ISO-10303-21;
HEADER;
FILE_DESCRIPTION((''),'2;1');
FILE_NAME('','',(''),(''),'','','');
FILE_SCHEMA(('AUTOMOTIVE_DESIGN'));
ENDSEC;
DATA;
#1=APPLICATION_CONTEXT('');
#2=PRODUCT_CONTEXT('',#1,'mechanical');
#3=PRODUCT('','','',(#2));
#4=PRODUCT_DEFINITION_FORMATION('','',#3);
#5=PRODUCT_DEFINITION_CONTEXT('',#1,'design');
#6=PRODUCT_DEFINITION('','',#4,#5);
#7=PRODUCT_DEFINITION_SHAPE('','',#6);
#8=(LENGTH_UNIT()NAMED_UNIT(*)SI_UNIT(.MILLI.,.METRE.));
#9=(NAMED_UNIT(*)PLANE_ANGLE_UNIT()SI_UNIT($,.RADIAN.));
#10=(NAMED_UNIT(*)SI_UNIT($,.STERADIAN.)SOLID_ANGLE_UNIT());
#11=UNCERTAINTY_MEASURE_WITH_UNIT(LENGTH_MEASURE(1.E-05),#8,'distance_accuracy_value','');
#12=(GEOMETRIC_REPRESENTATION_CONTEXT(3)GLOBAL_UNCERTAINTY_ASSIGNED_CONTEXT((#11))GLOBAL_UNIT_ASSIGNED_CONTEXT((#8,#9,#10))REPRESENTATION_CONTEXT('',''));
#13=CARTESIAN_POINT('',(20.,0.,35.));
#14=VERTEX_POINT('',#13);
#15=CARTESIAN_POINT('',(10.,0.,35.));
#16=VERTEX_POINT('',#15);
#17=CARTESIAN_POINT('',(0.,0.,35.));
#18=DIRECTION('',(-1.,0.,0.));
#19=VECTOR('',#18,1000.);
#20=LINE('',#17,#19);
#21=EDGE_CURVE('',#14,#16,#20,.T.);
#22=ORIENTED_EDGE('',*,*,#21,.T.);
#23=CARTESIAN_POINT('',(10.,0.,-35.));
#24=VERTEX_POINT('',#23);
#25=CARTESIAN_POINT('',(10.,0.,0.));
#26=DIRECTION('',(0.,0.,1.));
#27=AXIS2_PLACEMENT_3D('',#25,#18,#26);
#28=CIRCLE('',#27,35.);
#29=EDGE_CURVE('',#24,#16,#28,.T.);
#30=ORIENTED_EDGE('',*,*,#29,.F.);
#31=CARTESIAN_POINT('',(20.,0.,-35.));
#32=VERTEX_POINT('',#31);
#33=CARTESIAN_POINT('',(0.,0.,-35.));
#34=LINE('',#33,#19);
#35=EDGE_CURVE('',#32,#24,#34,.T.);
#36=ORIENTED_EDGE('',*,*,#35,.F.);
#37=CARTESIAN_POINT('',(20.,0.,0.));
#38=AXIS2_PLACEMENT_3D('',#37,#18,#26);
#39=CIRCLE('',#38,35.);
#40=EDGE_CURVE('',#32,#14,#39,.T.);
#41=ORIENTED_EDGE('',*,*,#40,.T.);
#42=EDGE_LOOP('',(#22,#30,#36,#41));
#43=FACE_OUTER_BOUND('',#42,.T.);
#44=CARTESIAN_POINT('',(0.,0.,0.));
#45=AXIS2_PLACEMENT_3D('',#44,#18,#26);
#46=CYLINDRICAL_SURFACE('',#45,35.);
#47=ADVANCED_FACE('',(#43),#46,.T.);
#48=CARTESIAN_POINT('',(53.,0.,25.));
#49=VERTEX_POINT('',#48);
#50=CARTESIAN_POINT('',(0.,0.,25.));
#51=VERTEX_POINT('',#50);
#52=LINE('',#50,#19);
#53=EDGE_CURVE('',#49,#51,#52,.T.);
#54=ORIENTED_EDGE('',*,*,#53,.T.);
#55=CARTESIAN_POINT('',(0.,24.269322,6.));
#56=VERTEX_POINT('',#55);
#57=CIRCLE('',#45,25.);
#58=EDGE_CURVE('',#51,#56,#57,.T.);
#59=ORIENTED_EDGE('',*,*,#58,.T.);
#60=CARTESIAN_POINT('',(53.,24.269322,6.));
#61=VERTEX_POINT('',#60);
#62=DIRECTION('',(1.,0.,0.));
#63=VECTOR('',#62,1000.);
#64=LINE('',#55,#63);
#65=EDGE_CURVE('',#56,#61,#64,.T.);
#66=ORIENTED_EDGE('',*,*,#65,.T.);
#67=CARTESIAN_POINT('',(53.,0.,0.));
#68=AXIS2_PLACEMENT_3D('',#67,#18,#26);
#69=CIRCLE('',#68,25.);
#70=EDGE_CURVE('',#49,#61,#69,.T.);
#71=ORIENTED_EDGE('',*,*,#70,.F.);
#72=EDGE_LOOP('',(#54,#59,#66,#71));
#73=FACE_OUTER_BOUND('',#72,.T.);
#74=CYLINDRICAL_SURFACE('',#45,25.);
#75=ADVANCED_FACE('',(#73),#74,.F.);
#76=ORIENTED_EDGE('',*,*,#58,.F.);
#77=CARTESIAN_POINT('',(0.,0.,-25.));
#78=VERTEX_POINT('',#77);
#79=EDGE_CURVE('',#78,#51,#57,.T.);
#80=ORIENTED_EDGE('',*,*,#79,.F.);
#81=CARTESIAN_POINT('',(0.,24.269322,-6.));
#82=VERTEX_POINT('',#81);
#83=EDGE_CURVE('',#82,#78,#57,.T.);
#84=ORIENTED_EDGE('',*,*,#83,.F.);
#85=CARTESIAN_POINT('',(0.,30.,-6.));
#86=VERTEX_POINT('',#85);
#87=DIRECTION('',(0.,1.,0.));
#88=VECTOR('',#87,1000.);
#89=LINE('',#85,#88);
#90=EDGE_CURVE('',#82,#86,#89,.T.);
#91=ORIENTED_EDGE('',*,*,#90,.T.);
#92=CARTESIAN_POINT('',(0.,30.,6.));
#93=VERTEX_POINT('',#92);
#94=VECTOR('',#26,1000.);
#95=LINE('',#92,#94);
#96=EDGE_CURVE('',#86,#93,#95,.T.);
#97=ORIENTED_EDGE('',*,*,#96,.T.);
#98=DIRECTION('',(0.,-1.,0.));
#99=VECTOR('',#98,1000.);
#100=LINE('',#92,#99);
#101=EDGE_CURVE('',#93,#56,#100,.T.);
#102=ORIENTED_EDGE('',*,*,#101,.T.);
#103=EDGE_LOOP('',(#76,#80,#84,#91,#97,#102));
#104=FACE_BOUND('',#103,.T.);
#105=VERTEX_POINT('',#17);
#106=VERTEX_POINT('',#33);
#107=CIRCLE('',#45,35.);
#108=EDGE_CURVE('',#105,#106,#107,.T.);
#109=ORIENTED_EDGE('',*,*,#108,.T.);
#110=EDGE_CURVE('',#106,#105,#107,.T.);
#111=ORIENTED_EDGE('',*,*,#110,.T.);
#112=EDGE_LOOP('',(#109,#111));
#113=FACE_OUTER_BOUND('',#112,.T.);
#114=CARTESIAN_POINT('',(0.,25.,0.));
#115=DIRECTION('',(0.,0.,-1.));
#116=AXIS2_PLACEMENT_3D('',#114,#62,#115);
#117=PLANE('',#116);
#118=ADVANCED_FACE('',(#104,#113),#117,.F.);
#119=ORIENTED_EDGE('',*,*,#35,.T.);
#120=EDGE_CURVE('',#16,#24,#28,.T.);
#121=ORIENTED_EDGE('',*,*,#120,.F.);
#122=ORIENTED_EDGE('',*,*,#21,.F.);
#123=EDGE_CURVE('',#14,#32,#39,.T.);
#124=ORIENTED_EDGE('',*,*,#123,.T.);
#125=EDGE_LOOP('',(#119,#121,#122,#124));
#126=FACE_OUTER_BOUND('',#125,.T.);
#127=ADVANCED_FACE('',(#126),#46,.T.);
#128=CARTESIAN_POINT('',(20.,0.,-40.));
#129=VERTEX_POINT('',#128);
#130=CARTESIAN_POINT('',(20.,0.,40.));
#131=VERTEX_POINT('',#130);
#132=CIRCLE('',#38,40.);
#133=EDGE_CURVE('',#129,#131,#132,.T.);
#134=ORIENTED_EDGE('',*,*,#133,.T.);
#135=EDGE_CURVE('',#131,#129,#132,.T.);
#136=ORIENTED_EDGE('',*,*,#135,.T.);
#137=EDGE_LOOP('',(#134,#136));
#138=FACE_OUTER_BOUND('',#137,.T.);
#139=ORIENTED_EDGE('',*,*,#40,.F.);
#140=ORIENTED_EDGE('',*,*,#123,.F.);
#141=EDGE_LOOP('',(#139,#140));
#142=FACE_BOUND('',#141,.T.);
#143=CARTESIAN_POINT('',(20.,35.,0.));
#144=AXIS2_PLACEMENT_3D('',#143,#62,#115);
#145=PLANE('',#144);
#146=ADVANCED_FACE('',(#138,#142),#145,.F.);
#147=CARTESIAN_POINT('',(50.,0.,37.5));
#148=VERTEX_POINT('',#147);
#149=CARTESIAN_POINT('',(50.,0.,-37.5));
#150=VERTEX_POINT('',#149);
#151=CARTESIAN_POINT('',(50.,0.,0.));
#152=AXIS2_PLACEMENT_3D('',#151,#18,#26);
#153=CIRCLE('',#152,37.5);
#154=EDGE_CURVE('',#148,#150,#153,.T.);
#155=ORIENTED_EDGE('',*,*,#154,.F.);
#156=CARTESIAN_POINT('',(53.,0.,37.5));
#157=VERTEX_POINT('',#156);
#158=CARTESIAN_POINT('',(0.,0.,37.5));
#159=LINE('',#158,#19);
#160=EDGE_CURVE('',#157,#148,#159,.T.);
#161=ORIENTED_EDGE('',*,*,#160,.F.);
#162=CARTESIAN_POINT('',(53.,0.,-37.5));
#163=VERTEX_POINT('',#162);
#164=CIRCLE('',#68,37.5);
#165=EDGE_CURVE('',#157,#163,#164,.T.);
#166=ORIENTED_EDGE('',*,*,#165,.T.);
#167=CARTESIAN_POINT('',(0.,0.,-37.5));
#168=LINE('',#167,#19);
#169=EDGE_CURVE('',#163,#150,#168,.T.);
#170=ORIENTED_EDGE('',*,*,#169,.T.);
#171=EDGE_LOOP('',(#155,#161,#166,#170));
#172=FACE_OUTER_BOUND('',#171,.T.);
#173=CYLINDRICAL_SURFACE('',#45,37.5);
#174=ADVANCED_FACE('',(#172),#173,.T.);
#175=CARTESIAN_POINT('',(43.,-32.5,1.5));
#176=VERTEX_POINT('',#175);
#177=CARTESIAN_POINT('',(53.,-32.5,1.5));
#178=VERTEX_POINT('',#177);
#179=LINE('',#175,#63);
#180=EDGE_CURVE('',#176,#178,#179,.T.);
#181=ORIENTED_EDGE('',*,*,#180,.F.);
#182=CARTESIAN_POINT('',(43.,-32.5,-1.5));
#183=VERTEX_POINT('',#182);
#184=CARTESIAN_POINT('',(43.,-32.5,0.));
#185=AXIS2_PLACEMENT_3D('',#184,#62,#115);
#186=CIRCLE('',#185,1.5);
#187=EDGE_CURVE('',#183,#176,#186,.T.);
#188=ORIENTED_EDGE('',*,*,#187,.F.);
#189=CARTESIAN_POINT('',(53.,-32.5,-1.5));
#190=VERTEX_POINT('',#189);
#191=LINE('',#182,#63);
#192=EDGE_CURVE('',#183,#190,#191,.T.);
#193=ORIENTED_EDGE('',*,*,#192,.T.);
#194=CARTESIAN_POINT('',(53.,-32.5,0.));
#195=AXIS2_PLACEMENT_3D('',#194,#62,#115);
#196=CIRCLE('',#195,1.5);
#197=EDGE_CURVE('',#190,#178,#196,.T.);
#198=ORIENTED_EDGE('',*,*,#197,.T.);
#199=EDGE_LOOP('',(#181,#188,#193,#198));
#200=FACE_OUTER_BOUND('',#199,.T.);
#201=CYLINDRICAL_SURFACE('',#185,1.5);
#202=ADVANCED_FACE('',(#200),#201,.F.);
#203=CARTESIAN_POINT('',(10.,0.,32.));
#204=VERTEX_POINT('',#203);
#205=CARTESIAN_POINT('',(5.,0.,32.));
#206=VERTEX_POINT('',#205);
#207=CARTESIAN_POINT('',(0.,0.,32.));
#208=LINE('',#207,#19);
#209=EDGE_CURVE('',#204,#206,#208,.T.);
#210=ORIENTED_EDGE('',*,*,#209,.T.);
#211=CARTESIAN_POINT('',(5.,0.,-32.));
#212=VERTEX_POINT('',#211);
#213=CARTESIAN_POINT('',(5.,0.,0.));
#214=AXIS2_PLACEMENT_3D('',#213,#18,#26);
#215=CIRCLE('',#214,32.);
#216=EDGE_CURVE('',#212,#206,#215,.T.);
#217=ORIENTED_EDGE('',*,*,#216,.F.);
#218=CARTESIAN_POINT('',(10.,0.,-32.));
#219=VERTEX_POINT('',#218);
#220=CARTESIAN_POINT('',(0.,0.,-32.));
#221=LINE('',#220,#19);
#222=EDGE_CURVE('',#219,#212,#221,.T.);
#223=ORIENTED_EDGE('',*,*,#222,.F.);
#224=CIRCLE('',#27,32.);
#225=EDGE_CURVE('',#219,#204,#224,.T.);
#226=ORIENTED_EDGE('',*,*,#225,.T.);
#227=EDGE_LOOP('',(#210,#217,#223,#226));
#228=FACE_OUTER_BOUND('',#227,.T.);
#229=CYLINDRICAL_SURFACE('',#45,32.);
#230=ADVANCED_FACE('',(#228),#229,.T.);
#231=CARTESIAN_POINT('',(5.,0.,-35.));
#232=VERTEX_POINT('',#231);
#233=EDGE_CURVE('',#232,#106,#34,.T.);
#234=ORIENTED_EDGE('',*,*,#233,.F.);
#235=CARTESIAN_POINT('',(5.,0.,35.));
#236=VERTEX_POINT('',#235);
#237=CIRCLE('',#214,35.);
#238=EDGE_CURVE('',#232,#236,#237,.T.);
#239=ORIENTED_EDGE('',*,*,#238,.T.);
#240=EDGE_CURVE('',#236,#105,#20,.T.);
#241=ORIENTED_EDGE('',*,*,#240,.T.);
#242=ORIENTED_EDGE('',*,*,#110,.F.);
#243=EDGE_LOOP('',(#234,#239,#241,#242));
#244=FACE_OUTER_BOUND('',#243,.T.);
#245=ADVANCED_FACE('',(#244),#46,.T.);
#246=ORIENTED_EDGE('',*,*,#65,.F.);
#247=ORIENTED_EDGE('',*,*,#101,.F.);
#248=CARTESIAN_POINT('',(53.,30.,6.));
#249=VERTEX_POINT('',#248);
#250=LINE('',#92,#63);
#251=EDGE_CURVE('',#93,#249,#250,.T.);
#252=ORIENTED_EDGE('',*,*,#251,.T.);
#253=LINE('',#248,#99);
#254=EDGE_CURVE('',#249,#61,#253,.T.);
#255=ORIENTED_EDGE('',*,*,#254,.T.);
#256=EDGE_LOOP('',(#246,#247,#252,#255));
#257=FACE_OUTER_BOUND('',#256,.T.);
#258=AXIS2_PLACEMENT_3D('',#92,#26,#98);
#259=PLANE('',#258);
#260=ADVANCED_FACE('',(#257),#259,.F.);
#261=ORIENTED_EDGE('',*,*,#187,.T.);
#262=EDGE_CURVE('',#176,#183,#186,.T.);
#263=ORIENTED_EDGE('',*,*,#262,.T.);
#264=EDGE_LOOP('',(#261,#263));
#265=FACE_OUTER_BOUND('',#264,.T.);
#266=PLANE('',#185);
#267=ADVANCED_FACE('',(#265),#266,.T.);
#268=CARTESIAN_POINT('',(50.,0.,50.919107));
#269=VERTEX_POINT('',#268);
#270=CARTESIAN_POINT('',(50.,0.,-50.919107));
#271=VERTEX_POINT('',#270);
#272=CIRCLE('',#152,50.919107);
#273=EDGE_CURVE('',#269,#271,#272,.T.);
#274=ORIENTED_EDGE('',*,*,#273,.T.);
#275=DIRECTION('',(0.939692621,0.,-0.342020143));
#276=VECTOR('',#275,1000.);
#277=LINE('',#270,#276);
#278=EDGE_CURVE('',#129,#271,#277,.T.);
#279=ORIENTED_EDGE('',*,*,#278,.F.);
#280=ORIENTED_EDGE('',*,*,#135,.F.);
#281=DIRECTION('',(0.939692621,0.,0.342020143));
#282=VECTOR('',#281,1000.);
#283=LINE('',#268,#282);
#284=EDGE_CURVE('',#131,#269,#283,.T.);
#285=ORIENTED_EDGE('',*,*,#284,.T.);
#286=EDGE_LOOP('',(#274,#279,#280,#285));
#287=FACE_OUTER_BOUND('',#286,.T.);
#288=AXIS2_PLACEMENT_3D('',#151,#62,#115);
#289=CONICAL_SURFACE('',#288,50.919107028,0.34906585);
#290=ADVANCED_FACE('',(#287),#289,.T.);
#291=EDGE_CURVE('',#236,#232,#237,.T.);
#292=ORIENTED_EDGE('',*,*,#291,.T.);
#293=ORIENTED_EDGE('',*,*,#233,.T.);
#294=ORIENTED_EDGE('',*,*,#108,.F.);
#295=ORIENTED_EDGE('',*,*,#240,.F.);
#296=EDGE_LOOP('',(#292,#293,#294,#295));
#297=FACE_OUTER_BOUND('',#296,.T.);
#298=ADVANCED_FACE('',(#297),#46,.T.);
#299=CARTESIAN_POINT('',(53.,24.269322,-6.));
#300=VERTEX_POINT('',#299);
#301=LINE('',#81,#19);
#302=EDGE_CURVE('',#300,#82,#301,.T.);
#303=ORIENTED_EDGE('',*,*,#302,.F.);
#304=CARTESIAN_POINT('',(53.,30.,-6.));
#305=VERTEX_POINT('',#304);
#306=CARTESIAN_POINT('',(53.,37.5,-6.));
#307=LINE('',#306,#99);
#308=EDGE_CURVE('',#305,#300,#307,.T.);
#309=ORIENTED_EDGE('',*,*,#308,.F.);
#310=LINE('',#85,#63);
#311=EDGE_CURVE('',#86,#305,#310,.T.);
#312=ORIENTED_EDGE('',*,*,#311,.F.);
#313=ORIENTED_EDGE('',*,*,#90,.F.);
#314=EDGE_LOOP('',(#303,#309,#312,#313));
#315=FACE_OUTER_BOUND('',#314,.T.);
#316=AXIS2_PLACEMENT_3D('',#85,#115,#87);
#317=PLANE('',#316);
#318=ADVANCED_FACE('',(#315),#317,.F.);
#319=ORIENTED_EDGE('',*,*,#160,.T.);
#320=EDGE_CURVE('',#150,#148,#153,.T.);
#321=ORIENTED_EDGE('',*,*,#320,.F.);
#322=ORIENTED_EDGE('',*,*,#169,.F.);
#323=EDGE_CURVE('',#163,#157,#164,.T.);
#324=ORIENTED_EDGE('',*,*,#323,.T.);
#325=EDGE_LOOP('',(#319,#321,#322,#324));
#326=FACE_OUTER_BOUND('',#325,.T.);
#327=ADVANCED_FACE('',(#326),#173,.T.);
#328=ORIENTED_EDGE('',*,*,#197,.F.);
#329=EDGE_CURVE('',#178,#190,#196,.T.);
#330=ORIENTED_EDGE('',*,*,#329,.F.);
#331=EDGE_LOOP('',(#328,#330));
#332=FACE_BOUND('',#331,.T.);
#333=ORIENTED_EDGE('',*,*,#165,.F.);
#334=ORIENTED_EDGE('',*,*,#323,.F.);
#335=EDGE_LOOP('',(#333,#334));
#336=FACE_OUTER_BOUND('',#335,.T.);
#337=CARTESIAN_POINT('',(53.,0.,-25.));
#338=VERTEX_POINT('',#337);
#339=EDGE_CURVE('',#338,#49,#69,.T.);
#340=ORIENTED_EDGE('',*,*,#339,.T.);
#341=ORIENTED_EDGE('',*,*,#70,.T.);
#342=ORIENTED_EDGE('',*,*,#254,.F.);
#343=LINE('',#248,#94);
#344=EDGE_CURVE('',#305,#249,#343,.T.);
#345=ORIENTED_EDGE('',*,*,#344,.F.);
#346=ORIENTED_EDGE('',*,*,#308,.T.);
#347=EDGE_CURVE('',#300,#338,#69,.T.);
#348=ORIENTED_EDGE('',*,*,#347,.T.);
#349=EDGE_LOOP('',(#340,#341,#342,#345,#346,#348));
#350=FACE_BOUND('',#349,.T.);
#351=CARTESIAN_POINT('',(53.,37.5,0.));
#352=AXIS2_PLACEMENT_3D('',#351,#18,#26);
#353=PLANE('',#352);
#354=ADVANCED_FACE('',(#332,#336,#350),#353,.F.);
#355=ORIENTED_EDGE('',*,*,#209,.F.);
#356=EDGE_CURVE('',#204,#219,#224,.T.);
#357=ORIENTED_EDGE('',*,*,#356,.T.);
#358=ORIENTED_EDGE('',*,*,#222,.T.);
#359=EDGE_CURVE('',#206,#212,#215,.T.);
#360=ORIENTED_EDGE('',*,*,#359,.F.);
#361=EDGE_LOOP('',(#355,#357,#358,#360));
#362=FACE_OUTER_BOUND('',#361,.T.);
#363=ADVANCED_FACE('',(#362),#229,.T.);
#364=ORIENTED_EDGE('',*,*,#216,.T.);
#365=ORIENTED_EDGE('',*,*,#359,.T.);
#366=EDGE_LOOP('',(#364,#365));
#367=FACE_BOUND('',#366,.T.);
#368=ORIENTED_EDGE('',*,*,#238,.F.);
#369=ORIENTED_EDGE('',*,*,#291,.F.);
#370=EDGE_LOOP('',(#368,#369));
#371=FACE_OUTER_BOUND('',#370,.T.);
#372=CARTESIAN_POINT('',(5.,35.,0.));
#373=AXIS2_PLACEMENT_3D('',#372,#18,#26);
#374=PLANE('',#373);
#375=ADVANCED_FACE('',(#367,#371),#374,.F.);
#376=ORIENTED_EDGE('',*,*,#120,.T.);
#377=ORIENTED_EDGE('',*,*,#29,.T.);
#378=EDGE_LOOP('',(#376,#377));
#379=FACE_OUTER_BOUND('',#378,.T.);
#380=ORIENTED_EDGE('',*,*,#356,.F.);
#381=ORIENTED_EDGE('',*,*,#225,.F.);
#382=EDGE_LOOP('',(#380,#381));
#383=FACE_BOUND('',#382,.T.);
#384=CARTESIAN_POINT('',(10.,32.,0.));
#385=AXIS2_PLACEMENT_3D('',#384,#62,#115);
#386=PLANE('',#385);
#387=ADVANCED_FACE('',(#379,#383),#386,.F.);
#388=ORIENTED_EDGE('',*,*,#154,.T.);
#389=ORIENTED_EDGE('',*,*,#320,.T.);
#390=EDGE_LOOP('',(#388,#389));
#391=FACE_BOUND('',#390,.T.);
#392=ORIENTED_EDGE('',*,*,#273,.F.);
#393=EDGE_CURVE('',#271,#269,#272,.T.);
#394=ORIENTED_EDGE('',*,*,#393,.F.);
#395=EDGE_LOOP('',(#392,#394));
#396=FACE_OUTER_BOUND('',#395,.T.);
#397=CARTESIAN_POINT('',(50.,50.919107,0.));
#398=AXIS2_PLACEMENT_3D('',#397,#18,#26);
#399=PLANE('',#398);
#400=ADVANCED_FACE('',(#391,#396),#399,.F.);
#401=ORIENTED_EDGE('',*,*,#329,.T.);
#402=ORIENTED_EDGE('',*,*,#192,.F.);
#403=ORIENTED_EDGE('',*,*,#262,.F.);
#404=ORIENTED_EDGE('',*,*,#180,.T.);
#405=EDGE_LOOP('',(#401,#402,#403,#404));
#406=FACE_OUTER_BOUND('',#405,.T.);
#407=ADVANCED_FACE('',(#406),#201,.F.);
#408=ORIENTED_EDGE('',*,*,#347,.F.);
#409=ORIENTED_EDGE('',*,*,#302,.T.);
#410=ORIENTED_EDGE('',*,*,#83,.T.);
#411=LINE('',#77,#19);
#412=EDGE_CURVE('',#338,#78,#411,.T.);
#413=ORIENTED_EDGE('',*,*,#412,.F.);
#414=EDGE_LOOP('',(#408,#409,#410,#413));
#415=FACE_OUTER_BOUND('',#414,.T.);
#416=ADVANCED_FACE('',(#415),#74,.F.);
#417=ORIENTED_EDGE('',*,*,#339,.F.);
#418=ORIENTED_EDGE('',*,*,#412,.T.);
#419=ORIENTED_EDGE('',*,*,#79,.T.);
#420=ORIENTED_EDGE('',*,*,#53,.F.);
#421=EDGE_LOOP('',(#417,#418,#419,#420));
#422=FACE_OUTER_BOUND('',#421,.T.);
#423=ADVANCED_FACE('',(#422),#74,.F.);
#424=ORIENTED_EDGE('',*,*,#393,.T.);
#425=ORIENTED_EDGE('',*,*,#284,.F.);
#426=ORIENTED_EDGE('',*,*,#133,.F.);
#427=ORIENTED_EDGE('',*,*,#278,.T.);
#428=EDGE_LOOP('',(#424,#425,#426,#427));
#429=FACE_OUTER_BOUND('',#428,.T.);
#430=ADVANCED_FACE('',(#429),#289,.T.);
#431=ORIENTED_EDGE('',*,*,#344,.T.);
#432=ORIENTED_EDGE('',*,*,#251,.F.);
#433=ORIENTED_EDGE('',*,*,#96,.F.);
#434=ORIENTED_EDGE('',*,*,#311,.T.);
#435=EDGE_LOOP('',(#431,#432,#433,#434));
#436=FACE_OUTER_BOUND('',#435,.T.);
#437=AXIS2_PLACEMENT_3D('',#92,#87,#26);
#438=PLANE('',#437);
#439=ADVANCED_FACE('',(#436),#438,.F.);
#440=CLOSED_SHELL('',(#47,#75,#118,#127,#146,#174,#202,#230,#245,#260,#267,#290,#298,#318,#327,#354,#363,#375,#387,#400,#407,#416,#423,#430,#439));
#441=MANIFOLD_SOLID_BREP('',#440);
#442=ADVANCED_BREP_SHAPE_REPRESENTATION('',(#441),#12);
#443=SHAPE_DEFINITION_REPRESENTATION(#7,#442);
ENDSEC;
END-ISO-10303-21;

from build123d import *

# Parameters (mm, degrees)
SKETCH2_W          = 12
SKETCH2_H          = 12
CUT_EXTRUDE1_DEPTH = 90.412028951
SKETCH3_R          = 1.5
CUT_EXTRUDE2_DEPTH = 10


with BuildPart() as part:
    # Sketch1 → Revolve1 (revolve)
    with BuildSketch(Plane.XY, mode=Mode.PRIVATE) as revolve1_sk:
        Polygon((0, 25), (0, 35), (5, 35), (5, 32), (10, 32), (10, 35), (20, 35), (20, 40), (50, 50.919107028), (50, 37.5), (53, 37.5), (53, 25), align=None)
    revolve(revolve1_sk.sketch.rotate(Axis((0, 0, 0), (1, 0, 0)), 90), axis=Axis((0, 0, 0), (1, 0, 0)))

    # Sketch2 → Cut-Extrude1 (cut, through all)
    with BuildSketch(Plane(origin=(53, 0, 0), x_dir=(0, 0, -1), z_dir=(1, 0, 0))):
        with Locations((0, 24)):
            Rectangle(SKETCH2_W, SKETCH2_H)
    extrude(amount=-CUT_EXTRUDE1_DEPTH, mode=Mode.SUBTRACT)

    # Sketch3 → Cut-Extrude2 (cut)
    with BuildSketch(Plane(origin=(53, 0, 0), x_dir=(0, 0, -1), z_dir=(1, 0, 0))):
        with Locations((0, -32.5)):
            Circle(SKETCH3_R)
    extrude(amount=-CUT_EXTRUDE2_DEPTH, mode=Mode.SUBTRACT)


solid = part.part
